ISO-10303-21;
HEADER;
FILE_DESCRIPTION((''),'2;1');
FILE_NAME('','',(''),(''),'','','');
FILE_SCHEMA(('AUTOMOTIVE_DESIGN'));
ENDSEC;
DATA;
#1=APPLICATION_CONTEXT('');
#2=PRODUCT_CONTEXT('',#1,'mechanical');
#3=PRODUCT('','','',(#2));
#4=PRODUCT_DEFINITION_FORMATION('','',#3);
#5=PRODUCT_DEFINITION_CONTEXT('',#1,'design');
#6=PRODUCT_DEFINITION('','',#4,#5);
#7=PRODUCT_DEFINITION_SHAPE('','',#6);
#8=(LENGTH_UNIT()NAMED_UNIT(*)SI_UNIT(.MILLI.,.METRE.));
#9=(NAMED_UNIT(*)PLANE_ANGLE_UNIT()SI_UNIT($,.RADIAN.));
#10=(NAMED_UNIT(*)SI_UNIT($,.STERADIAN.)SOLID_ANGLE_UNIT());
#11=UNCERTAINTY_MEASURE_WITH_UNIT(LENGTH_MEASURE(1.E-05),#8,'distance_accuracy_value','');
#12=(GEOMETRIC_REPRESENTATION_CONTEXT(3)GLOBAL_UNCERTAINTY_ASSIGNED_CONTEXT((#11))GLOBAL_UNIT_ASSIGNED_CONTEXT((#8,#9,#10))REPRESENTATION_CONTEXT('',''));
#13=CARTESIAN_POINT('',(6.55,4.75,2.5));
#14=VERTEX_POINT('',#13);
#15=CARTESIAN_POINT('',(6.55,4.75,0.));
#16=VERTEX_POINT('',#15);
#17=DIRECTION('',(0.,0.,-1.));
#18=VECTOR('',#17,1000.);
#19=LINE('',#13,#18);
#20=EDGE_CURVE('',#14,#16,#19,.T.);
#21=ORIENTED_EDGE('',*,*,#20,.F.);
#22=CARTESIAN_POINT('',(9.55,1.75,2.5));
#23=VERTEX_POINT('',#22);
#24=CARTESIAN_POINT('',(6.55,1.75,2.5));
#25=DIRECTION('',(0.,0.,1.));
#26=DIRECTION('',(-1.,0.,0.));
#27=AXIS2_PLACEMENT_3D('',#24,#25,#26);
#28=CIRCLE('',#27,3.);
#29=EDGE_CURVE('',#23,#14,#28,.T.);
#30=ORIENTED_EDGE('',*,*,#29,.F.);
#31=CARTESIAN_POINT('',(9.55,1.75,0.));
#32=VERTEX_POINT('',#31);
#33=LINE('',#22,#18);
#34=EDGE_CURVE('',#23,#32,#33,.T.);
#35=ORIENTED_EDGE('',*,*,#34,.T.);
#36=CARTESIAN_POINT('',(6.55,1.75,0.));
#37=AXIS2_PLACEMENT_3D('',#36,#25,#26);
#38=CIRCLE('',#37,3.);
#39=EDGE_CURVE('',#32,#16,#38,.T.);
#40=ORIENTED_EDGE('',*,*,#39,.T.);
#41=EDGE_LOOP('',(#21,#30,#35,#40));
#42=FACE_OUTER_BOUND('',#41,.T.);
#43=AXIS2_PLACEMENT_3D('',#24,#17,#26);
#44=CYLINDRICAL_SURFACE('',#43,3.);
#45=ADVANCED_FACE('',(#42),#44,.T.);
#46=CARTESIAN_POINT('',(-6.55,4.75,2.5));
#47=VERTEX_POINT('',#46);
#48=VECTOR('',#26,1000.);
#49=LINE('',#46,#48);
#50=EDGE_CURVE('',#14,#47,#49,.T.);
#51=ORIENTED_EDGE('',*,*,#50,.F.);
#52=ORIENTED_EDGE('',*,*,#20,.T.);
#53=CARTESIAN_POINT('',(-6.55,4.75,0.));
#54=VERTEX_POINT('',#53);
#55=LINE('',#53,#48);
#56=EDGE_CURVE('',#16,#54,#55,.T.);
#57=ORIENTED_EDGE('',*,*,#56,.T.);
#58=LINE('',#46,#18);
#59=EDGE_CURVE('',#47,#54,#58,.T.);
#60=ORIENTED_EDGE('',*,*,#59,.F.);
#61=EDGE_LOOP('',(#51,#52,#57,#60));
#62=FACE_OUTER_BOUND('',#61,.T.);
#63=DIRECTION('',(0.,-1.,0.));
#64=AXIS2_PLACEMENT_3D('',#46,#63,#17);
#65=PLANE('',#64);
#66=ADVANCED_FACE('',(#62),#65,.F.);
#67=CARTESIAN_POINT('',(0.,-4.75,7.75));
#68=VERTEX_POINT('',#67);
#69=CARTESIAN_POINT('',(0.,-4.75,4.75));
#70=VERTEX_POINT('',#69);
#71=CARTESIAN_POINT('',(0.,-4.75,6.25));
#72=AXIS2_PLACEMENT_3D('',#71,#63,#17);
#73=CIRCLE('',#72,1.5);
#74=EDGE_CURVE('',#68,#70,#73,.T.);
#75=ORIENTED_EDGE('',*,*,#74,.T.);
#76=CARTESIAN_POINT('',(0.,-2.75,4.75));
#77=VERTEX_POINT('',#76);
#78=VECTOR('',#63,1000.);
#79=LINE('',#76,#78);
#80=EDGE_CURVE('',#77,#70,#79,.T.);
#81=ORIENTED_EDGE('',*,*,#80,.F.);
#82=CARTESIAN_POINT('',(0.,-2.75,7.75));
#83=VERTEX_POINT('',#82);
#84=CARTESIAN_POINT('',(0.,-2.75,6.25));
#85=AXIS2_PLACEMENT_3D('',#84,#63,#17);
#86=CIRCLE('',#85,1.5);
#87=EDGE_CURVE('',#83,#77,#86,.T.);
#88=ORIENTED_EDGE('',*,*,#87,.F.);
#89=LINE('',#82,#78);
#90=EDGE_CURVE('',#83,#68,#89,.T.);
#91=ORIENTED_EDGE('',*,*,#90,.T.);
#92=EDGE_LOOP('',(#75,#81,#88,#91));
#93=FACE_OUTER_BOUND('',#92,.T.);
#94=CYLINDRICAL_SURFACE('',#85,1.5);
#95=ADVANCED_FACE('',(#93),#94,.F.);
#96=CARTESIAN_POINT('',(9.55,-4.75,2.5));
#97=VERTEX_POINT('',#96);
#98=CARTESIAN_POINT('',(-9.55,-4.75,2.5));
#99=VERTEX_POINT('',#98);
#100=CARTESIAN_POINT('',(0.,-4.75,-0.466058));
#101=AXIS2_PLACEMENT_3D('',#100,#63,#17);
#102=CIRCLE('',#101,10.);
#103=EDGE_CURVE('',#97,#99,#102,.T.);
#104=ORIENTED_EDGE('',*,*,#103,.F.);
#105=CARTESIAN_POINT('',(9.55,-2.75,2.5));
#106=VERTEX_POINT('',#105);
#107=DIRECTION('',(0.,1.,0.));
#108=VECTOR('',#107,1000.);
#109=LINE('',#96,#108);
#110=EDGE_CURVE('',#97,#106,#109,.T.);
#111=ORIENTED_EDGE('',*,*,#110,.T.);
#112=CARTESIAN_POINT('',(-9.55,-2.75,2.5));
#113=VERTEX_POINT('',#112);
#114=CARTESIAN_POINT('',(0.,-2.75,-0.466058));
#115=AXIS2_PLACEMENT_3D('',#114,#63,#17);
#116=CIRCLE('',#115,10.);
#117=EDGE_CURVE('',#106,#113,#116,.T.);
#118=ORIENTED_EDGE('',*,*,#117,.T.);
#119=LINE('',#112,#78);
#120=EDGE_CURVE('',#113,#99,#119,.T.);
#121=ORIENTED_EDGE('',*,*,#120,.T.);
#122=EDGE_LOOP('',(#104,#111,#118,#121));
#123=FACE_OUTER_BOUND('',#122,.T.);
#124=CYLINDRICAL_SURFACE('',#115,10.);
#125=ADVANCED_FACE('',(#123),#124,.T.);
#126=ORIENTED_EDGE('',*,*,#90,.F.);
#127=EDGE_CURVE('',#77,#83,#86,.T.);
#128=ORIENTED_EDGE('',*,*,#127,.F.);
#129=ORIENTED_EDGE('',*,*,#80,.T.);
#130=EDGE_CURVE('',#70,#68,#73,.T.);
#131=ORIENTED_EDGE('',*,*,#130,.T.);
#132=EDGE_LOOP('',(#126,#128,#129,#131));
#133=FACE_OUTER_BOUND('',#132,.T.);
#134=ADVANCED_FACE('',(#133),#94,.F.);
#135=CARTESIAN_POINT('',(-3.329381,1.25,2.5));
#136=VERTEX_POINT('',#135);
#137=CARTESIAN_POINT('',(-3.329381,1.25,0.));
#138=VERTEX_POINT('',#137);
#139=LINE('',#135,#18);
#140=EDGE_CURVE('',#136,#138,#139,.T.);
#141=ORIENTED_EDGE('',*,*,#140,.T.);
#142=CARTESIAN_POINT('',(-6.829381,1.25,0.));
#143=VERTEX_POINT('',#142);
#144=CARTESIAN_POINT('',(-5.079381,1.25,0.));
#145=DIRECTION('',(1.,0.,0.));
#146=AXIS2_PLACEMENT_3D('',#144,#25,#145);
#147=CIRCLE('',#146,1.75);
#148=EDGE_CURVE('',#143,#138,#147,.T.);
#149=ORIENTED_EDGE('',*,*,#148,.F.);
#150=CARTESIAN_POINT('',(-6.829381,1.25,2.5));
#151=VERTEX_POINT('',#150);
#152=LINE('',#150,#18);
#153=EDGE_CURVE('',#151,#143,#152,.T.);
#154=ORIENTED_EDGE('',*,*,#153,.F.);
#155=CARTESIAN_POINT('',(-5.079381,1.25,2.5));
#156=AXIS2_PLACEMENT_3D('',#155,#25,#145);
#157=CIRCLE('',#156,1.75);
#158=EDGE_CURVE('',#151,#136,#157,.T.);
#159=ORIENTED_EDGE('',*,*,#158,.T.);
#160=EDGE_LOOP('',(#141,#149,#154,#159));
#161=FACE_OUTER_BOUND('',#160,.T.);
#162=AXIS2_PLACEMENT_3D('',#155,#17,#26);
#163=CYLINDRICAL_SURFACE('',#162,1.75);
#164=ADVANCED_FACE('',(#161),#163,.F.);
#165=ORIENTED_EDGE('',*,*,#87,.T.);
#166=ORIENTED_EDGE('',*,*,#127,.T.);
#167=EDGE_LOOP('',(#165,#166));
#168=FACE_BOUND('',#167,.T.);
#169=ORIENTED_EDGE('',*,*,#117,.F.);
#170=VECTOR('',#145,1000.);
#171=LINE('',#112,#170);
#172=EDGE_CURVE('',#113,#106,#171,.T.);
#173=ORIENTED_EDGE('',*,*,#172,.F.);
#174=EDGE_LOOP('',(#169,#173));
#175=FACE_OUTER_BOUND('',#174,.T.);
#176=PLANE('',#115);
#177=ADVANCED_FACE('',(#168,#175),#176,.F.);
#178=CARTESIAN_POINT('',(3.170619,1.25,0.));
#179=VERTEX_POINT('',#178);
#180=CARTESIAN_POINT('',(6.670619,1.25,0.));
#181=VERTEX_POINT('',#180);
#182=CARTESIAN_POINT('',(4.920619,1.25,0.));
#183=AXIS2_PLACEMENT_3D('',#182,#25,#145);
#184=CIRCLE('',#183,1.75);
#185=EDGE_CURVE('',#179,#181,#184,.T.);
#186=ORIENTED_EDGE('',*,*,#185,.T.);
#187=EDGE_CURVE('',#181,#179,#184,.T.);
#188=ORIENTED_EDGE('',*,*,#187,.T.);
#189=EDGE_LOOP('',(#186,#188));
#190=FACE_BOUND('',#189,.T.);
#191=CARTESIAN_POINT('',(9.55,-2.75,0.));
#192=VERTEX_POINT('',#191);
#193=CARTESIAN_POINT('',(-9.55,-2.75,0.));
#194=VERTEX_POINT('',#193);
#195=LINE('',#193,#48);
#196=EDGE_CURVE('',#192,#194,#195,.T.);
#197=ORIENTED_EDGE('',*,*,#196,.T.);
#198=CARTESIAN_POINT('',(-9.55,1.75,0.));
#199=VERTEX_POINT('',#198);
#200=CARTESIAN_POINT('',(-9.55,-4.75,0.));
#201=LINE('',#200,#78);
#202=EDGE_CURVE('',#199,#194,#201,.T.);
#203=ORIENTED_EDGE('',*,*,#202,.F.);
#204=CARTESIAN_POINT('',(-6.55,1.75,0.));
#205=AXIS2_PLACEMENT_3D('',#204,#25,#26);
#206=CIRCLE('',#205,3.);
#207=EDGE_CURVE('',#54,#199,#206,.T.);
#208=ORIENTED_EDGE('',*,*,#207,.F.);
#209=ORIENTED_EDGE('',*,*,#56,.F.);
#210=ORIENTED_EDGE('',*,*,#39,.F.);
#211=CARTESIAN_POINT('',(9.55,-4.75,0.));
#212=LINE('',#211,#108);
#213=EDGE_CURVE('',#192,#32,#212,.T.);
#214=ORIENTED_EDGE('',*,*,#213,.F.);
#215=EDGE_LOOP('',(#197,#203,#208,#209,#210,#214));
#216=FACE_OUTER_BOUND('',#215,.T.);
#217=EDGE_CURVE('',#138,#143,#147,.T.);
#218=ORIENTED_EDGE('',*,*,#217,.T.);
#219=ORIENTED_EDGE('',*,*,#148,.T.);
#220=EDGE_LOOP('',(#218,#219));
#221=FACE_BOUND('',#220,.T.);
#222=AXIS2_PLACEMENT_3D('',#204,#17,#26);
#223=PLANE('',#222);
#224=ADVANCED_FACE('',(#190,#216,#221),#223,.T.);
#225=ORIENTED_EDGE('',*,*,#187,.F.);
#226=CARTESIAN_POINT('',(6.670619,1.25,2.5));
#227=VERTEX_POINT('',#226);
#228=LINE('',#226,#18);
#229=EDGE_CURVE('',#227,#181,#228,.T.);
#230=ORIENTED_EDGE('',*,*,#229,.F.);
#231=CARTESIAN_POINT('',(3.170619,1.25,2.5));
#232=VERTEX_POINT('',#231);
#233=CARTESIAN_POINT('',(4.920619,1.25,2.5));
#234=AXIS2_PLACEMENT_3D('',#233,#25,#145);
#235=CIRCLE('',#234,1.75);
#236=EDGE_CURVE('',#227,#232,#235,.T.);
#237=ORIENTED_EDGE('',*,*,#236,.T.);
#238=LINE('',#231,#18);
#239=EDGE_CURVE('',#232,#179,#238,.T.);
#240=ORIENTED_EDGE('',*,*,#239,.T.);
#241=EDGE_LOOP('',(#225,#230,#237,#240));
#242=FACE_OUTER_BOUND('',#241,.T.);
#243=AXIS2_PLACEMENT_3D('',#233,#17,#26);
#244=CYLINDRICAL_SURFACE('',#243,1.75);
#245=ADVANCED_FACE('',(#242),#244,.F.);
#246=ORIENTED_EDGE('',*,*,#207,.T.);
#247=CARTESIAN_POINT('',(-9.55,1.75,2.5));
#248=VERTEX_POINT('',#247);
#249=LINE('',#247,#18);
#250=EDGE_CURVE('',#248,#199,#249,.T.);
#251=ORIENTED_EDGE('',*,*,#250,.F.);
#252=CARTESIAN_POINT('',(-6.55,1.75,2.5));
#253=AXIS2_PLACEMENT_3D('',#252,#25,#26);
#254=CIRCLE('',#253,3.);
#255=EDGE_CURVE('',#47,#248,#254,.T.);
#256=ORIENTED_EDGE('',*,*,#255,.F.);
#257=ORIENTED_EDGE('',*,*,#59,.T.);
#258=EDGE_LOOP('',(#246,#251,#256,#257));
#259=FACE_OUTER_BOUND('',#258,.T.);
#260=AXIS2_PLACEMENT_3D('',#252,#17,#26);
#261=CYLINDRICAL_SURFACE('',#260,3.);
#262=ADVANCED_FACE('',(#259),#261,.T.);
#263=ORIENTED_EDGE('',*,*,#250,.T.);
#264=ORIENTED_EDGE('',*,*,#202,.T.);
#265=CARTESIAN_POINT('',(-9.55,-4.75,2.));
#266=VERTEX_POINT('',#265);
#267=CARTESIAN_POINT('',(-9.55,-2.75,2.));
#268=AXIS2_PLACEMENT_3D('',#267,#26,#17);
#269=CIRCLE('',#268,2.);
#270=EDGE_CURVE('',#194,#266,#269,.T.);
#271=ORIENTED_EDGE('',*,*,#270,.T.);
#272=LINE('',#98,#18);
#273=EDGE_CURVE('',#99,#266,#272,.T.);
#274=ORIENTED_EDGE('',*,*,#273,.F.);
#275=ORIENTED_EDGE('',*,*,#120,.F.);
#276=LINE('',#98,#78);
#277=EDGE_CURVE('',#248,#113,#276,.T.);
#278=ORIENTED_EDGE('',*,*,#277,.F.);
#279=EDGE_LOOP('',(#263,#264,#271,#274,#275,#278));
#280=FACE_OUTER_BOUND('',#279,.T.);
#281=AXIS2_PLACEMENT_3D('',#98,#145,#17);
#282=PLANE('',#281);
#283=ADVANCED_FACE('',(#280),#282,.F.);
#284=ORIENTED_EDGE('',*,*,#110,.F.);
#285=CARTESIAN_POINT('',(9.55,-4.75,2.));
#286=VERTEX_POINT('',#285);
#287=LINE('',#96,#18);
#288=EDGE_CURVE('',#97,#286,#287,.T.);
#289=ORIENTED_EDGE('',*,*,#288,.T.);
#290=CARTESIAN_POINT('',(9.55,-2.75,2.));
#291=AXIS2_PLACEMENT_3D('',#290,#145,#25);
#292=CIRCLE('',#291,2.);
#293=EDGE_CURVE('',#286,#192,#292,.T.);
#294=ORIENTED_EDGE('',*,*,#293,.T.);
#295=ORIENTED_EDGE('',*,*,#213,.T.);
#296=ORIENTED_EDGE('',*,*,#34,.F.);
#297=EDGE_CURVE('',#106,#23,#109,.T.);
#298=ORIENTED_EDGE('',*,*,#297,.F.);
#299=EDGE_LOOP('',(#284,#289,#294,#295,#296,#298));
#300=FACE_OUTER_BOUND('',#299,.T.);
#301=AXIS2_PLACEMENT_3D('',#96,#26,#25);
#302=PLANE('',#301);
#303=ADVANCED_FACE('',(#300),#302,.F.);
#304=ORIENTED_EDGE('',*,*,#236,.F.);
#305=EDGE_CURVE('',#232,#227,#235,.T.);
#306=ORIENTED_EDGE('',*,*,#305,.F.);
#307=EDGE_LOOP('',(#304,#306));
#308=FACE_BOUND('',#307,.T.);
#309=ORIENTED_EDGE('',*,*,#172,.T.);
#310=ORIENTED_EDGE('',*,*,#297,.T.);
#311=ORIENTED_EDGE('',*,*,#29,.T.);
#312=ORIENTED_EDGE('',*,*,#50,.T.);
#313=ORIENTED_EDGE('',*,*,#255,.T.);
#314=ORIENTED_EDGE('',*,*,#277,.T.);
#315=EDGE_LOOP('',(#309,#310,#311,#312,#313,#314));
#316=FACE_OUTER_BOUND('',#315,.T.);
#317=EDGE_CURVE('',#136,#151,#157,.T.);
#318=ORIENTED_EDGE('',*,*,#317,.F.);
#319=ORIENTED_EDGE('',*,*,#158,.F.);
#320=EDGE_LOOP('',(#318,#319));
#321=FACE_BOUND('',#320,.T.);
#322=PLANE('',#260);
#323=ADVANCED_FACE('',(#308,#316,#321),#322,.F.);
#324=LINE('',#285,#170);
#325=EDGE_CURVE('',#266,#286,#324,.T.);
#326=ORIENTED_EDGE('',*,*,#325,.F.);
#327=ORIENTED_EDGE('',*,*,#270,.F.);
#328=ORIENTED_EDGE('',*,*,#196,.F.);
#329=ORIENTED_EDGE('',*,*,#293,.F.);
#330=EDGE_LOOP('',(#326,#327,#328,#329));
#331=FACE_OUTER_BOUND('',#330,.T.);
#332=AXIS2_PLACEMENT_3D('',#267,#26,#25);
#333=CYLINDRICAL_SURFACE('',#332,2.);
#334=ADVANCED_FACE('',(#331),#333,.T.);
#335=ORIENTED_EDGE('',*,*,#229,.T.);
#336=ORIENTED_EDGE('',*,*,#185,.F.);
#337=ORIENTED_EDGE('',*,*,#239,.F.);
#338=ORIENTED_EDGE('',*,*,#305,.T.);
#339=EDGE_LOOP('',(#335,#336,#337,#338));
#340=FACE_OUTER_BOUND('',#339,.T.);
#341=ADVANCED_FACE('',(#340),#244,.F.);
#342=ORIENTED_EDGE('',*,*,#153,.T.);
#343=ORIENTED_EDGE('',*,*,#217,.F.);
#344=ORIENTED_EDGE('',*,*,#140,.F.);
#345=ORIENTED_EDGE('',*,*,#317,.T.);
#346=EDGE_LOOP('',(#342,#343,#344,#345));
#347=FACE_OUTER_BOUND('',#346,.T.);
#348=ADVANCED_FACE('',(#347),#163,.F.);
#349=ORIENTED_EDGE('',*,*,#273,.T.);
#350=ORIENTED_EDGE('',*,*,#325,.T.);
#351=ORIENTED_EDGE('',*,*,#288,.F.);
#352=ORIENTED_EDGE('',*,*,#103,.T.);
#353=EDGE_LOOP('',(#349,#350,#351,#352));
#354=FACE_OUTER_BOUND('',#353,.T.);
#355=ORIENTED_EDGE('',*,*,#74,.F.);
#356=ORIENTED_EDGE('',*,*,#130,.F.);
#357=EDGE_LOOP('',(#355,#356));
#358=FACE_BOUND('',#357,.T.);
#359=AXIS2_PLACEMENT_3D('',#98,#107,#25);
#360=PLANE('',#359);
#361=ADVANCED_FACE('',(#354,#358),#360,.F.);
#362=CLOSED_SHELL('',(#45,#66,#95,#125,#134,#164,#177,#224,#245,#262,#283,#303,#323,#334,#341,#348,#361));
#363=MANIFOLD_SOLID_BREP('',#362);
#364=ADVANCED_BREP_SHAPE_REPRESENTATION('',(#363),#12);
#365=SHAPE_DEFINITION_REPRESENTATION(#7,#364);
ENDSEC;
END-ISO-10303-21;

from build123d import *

# Parameters (mm, degrees)
SKETCH_1_R      = 1.75
EXTRUDE_1_DEPTH = 2.5
SKETCH_2_R      = 1.5
EXTRUDE_2_DEPTH = 2
FILLET_1_R      = 2


with BuildPart() as part:
    # 草图1 → 凸台-拉伸1 (new body)
    with BuildSketch(Plane.XY):
        with BuildLine():
            Line((-9.55, -4.75), (9.55, -4.75))
            Line((9.55, -4.75), (9.55, 1.75))
            ThreePointArc((9.55, 1.75), (8.671320344, 3.871320344), (6.55, 4.75))
            Line((6.55, 4.75), (-6.55, 4.75))
            ThreePointArc((-6.55, 4.75), (-8.671320344, 3.871320344), (-9.55, 1.75))
            Line((-9.55, 1.75), (-9.55, -4.75))
        make_face()
        with Locations((4.920618816, 1.25)):
            Circle(SKETCH_1_R, mode=Mode.SUBTRACT)
        with Locations((-5.079381184, 1.25)):
            Circle(SKETCH_1_R, mode=Mode.SUBTRACT)
    extrude(amount=EXTRUDE_1_DEPTH)

    # 草图2 → 凸台-拉伸2 (add)
    with BuildSketch(Plane.XZ.offset(4.75)):
        with BuildLine():
            Line((-9.55, 2.5), (9.55, 2.5))
            ThreePointArc((9.55, 2.5), (0, 9.53394201), (-9.55, 2.5))
        make_face()
        with Locations(Location((0, 6.25, 0), (0, 0, 270))):
            Circle(SKETCH_2_R, mode=Mode.SUBTRACT)
    extrude(amount=-EXTRUDE_2_DEPTH)

    # 圆角1
    fillet_1_edges = [part.edges().sort_by_distance(p)[0] for p in [
        (0, -4.75, 0),
    ]]
    fillet(fillet_1_edges, radius=FILLET_1_R)


solid = part.part
